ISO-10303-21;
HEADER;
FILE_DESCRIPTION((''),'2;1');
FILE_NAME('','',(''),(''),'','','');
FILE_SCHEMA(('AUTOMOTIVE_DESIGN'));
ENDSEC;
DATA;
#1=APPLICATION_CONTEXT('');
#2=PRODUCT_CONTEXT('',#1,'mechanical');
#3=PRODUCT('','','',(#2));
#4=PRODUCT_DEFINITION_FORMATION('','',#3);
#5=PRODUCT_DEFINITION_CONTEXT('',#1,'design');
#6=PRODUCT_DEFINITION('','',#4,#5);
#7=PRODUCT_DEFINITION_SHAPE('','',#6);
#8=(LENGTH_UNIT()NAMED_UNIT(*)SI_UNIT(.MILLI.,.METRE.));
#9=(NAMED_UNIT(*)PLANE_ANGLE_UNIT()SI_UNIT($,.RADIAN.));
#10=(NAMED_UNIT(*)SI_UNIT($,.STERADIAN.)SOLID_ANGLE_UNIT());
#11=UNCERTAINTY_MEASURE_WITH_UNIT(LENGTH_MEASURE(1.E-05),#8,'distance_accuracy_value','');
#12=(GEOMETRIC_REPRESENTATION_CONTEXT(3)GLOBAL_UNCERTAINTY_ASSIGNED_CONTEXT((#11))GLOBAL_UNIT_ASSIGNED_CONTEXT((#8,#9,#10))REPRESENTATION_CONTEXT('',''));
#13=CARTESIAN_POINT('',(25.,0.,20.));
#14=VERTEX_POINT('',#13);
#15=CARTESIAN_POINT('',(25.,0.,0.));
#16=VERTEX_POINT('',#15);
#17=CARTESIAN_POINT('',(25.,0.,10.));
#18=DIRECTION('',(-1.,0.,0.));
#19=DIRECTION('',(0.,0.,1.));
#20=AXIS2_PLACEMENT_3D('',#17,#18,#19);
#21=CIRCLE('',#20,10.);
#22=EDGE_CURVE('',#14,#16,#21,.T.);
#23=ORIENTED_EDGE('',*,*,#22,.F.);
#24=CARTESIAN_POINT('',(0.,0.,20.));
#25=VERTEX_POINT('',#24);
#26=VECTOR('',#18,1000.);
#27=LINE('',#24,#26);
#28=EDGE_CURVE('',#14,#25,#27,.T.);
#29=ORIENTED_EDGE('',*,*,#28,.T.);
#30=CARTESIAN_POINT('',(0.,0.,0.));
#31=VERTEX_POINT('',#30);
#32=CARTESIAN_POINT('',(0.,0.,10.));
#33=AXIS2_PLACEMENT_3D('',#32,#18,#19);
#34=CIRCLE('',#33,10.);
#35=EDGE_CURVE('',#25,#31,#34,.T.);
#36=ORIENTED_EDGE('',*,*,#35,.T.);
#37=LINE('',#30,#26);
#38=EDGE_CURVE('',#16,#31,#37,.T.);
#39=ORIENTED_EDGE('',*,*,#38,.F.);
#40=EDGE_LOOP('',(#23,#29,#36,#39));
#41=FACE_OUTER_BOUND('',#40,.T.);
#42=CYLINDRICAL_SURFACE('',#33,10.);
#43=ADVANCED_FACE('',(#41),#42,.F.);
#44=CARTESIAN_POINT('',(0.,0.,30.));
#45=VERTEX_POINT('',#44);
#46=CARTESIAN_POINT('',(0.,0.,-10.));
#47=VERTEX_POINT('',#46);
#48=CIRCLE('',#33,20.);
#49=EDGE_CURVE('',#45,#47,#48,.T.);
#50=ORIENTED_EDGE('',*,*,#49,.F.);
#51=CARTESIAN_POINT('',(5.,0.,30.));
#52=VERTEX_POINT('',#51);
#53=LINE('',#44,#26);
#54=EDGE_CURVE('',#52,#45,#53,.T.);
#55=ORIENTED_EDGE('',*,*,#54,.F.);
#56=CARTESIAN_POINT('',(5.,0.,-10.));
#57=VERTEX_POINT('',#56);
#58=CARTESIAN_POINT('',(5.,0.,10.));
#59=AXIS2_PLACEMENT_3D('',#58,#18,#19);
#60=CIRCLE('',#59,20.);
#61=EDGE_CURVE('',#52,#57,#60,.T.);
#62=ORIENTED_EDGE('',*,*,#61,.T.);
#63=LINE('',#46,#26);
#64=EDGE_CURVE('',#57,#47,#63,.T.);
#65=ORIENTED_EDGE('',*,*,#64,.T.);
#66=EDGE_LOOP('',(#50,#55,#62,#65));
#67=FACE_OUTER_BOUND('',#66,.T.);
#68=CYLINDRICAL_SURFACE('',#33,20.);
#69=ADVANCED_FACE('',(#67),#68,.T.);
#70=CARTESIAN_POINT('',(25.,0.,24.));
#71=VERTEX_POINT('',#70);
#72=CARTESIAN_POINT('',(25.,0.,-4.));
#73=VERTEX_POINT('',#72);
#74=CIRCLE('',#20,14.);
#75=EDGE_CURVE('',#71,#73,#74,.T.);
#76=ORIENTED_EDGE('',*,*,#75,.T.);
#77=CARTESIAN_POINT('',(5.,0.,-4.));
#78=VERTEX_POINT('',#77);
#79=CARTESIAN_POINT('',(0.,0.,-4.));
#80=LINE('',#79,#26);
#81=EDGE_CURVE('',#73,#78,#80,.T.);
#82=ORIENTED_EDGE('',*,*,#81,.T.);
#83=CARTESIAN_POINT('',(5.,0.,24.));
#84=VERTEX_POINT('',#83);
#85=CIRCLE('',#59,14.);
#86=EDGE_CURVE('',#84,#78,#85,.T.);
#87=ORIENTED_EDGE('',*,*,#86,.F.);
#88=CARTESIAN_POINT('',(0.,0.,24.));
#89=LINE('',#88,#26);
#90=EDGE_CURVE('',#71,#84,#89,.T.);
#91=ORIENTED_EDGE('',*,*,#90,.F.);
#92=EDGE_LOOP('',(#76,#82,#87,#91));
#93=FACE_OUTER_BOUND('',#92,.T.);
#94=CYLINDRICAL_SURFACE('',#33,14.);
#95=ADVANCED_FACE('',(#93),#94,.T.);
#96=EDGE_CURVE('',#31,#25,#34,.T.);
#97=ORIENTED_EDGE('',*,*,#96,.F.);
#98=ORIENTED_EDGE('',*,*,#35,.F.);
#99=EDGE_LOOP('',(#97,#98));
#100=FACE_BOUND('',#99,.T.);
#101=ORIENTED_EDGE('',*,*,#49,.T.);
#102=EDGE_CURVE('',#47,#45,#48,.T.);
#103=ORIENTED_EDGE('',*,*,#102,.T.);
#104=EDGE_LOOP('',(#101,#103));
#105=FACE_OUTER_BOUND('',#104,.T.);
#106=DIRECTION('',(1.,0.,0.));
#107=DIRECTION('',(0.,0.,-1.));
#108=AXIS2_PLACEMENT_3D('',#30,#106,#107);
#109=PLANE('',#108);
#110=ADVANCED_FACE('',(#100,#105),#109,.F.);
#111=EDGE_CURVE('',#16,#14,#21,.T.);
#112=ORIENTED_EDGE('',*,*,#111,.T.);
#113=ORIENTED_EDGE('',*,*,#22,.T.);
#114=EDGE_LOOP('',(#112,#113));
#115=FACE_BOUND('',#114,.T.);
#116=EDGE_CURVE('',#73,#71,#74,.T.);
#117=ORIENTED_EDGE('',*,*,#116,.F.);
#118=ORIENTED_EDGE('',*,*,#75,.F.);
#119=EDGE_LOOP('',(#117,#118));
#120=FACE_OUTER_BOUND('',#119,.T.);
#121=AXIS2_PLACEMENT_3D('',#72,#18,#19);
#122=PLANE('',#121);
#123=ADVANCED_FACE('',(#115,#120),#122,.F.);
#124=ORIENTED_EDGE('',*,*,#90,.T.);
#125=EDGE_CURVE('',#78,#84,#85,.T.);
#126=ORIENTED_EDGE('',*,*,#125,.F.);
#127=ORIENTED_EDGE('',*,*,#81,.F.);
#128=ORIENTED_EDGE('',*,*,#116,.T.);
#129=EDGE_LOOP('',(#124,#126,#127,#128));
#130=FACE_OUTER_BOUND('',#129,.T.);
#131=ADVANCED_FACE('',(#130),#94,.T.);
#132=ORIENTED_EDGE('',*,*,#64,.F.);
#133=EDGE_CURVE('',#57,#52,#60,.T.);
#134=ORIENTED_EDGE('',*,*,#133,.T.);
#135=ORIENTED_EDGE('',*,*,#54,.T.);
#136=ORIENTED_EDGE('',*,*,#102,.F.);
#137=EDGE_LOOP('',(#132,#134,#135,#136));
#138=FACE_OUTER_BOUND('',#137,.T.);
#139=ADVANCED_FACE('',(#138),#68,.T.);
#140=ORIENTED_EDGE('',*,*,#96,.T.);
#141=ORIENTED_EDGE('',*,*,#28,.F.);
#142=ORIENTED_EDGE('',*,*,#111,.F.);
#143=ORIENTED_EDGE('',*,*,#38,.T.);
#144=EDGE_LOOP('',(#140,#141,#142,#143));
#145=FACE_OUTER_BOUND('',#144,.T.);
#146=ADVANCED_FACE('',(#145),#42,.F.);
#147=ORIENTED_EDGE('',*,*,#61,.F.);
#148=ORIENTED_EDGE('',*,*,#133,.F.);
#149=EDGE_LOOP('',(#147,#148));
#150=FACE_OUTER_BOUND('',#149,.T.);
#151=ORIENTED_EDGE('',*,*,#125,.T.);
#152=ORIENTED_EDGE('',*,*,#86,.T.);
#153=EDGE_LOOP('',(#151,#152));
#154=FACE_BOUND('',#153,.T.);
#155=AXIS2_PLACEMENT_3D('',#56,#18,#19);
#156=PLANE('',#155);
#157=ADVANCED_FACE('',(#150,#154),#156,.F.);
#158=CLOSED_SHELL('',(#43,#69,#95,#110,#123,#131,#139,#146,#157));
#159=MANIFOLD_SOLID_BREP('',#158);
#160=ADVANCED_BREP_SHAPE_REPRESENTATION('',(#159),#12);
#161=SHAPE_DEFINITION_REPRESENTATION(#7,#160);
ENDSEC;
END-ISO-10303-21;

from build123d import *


with BuildPart() as part:
    # Sketch1 → Revolve1 (revolve)
    with BuildSketch(Plane(origin=(0, 0, 0), x_dir=(1, 0, 0), z_dir=(0, 1, 0)), mode=Mode.PRIVATE) as revolve1_sk:
        Polygon((0, 0), (0, 10), (5, 10), (5, 4), (25, 4), (25, 0), align=None)
    revolve(revolve1_sk.sketch.rotate(Axis((0, 0, 10), (1, 0, 0)), 180), axis=Axis((0, 0, 10), (1, 0, 0)))


solid = part.part
